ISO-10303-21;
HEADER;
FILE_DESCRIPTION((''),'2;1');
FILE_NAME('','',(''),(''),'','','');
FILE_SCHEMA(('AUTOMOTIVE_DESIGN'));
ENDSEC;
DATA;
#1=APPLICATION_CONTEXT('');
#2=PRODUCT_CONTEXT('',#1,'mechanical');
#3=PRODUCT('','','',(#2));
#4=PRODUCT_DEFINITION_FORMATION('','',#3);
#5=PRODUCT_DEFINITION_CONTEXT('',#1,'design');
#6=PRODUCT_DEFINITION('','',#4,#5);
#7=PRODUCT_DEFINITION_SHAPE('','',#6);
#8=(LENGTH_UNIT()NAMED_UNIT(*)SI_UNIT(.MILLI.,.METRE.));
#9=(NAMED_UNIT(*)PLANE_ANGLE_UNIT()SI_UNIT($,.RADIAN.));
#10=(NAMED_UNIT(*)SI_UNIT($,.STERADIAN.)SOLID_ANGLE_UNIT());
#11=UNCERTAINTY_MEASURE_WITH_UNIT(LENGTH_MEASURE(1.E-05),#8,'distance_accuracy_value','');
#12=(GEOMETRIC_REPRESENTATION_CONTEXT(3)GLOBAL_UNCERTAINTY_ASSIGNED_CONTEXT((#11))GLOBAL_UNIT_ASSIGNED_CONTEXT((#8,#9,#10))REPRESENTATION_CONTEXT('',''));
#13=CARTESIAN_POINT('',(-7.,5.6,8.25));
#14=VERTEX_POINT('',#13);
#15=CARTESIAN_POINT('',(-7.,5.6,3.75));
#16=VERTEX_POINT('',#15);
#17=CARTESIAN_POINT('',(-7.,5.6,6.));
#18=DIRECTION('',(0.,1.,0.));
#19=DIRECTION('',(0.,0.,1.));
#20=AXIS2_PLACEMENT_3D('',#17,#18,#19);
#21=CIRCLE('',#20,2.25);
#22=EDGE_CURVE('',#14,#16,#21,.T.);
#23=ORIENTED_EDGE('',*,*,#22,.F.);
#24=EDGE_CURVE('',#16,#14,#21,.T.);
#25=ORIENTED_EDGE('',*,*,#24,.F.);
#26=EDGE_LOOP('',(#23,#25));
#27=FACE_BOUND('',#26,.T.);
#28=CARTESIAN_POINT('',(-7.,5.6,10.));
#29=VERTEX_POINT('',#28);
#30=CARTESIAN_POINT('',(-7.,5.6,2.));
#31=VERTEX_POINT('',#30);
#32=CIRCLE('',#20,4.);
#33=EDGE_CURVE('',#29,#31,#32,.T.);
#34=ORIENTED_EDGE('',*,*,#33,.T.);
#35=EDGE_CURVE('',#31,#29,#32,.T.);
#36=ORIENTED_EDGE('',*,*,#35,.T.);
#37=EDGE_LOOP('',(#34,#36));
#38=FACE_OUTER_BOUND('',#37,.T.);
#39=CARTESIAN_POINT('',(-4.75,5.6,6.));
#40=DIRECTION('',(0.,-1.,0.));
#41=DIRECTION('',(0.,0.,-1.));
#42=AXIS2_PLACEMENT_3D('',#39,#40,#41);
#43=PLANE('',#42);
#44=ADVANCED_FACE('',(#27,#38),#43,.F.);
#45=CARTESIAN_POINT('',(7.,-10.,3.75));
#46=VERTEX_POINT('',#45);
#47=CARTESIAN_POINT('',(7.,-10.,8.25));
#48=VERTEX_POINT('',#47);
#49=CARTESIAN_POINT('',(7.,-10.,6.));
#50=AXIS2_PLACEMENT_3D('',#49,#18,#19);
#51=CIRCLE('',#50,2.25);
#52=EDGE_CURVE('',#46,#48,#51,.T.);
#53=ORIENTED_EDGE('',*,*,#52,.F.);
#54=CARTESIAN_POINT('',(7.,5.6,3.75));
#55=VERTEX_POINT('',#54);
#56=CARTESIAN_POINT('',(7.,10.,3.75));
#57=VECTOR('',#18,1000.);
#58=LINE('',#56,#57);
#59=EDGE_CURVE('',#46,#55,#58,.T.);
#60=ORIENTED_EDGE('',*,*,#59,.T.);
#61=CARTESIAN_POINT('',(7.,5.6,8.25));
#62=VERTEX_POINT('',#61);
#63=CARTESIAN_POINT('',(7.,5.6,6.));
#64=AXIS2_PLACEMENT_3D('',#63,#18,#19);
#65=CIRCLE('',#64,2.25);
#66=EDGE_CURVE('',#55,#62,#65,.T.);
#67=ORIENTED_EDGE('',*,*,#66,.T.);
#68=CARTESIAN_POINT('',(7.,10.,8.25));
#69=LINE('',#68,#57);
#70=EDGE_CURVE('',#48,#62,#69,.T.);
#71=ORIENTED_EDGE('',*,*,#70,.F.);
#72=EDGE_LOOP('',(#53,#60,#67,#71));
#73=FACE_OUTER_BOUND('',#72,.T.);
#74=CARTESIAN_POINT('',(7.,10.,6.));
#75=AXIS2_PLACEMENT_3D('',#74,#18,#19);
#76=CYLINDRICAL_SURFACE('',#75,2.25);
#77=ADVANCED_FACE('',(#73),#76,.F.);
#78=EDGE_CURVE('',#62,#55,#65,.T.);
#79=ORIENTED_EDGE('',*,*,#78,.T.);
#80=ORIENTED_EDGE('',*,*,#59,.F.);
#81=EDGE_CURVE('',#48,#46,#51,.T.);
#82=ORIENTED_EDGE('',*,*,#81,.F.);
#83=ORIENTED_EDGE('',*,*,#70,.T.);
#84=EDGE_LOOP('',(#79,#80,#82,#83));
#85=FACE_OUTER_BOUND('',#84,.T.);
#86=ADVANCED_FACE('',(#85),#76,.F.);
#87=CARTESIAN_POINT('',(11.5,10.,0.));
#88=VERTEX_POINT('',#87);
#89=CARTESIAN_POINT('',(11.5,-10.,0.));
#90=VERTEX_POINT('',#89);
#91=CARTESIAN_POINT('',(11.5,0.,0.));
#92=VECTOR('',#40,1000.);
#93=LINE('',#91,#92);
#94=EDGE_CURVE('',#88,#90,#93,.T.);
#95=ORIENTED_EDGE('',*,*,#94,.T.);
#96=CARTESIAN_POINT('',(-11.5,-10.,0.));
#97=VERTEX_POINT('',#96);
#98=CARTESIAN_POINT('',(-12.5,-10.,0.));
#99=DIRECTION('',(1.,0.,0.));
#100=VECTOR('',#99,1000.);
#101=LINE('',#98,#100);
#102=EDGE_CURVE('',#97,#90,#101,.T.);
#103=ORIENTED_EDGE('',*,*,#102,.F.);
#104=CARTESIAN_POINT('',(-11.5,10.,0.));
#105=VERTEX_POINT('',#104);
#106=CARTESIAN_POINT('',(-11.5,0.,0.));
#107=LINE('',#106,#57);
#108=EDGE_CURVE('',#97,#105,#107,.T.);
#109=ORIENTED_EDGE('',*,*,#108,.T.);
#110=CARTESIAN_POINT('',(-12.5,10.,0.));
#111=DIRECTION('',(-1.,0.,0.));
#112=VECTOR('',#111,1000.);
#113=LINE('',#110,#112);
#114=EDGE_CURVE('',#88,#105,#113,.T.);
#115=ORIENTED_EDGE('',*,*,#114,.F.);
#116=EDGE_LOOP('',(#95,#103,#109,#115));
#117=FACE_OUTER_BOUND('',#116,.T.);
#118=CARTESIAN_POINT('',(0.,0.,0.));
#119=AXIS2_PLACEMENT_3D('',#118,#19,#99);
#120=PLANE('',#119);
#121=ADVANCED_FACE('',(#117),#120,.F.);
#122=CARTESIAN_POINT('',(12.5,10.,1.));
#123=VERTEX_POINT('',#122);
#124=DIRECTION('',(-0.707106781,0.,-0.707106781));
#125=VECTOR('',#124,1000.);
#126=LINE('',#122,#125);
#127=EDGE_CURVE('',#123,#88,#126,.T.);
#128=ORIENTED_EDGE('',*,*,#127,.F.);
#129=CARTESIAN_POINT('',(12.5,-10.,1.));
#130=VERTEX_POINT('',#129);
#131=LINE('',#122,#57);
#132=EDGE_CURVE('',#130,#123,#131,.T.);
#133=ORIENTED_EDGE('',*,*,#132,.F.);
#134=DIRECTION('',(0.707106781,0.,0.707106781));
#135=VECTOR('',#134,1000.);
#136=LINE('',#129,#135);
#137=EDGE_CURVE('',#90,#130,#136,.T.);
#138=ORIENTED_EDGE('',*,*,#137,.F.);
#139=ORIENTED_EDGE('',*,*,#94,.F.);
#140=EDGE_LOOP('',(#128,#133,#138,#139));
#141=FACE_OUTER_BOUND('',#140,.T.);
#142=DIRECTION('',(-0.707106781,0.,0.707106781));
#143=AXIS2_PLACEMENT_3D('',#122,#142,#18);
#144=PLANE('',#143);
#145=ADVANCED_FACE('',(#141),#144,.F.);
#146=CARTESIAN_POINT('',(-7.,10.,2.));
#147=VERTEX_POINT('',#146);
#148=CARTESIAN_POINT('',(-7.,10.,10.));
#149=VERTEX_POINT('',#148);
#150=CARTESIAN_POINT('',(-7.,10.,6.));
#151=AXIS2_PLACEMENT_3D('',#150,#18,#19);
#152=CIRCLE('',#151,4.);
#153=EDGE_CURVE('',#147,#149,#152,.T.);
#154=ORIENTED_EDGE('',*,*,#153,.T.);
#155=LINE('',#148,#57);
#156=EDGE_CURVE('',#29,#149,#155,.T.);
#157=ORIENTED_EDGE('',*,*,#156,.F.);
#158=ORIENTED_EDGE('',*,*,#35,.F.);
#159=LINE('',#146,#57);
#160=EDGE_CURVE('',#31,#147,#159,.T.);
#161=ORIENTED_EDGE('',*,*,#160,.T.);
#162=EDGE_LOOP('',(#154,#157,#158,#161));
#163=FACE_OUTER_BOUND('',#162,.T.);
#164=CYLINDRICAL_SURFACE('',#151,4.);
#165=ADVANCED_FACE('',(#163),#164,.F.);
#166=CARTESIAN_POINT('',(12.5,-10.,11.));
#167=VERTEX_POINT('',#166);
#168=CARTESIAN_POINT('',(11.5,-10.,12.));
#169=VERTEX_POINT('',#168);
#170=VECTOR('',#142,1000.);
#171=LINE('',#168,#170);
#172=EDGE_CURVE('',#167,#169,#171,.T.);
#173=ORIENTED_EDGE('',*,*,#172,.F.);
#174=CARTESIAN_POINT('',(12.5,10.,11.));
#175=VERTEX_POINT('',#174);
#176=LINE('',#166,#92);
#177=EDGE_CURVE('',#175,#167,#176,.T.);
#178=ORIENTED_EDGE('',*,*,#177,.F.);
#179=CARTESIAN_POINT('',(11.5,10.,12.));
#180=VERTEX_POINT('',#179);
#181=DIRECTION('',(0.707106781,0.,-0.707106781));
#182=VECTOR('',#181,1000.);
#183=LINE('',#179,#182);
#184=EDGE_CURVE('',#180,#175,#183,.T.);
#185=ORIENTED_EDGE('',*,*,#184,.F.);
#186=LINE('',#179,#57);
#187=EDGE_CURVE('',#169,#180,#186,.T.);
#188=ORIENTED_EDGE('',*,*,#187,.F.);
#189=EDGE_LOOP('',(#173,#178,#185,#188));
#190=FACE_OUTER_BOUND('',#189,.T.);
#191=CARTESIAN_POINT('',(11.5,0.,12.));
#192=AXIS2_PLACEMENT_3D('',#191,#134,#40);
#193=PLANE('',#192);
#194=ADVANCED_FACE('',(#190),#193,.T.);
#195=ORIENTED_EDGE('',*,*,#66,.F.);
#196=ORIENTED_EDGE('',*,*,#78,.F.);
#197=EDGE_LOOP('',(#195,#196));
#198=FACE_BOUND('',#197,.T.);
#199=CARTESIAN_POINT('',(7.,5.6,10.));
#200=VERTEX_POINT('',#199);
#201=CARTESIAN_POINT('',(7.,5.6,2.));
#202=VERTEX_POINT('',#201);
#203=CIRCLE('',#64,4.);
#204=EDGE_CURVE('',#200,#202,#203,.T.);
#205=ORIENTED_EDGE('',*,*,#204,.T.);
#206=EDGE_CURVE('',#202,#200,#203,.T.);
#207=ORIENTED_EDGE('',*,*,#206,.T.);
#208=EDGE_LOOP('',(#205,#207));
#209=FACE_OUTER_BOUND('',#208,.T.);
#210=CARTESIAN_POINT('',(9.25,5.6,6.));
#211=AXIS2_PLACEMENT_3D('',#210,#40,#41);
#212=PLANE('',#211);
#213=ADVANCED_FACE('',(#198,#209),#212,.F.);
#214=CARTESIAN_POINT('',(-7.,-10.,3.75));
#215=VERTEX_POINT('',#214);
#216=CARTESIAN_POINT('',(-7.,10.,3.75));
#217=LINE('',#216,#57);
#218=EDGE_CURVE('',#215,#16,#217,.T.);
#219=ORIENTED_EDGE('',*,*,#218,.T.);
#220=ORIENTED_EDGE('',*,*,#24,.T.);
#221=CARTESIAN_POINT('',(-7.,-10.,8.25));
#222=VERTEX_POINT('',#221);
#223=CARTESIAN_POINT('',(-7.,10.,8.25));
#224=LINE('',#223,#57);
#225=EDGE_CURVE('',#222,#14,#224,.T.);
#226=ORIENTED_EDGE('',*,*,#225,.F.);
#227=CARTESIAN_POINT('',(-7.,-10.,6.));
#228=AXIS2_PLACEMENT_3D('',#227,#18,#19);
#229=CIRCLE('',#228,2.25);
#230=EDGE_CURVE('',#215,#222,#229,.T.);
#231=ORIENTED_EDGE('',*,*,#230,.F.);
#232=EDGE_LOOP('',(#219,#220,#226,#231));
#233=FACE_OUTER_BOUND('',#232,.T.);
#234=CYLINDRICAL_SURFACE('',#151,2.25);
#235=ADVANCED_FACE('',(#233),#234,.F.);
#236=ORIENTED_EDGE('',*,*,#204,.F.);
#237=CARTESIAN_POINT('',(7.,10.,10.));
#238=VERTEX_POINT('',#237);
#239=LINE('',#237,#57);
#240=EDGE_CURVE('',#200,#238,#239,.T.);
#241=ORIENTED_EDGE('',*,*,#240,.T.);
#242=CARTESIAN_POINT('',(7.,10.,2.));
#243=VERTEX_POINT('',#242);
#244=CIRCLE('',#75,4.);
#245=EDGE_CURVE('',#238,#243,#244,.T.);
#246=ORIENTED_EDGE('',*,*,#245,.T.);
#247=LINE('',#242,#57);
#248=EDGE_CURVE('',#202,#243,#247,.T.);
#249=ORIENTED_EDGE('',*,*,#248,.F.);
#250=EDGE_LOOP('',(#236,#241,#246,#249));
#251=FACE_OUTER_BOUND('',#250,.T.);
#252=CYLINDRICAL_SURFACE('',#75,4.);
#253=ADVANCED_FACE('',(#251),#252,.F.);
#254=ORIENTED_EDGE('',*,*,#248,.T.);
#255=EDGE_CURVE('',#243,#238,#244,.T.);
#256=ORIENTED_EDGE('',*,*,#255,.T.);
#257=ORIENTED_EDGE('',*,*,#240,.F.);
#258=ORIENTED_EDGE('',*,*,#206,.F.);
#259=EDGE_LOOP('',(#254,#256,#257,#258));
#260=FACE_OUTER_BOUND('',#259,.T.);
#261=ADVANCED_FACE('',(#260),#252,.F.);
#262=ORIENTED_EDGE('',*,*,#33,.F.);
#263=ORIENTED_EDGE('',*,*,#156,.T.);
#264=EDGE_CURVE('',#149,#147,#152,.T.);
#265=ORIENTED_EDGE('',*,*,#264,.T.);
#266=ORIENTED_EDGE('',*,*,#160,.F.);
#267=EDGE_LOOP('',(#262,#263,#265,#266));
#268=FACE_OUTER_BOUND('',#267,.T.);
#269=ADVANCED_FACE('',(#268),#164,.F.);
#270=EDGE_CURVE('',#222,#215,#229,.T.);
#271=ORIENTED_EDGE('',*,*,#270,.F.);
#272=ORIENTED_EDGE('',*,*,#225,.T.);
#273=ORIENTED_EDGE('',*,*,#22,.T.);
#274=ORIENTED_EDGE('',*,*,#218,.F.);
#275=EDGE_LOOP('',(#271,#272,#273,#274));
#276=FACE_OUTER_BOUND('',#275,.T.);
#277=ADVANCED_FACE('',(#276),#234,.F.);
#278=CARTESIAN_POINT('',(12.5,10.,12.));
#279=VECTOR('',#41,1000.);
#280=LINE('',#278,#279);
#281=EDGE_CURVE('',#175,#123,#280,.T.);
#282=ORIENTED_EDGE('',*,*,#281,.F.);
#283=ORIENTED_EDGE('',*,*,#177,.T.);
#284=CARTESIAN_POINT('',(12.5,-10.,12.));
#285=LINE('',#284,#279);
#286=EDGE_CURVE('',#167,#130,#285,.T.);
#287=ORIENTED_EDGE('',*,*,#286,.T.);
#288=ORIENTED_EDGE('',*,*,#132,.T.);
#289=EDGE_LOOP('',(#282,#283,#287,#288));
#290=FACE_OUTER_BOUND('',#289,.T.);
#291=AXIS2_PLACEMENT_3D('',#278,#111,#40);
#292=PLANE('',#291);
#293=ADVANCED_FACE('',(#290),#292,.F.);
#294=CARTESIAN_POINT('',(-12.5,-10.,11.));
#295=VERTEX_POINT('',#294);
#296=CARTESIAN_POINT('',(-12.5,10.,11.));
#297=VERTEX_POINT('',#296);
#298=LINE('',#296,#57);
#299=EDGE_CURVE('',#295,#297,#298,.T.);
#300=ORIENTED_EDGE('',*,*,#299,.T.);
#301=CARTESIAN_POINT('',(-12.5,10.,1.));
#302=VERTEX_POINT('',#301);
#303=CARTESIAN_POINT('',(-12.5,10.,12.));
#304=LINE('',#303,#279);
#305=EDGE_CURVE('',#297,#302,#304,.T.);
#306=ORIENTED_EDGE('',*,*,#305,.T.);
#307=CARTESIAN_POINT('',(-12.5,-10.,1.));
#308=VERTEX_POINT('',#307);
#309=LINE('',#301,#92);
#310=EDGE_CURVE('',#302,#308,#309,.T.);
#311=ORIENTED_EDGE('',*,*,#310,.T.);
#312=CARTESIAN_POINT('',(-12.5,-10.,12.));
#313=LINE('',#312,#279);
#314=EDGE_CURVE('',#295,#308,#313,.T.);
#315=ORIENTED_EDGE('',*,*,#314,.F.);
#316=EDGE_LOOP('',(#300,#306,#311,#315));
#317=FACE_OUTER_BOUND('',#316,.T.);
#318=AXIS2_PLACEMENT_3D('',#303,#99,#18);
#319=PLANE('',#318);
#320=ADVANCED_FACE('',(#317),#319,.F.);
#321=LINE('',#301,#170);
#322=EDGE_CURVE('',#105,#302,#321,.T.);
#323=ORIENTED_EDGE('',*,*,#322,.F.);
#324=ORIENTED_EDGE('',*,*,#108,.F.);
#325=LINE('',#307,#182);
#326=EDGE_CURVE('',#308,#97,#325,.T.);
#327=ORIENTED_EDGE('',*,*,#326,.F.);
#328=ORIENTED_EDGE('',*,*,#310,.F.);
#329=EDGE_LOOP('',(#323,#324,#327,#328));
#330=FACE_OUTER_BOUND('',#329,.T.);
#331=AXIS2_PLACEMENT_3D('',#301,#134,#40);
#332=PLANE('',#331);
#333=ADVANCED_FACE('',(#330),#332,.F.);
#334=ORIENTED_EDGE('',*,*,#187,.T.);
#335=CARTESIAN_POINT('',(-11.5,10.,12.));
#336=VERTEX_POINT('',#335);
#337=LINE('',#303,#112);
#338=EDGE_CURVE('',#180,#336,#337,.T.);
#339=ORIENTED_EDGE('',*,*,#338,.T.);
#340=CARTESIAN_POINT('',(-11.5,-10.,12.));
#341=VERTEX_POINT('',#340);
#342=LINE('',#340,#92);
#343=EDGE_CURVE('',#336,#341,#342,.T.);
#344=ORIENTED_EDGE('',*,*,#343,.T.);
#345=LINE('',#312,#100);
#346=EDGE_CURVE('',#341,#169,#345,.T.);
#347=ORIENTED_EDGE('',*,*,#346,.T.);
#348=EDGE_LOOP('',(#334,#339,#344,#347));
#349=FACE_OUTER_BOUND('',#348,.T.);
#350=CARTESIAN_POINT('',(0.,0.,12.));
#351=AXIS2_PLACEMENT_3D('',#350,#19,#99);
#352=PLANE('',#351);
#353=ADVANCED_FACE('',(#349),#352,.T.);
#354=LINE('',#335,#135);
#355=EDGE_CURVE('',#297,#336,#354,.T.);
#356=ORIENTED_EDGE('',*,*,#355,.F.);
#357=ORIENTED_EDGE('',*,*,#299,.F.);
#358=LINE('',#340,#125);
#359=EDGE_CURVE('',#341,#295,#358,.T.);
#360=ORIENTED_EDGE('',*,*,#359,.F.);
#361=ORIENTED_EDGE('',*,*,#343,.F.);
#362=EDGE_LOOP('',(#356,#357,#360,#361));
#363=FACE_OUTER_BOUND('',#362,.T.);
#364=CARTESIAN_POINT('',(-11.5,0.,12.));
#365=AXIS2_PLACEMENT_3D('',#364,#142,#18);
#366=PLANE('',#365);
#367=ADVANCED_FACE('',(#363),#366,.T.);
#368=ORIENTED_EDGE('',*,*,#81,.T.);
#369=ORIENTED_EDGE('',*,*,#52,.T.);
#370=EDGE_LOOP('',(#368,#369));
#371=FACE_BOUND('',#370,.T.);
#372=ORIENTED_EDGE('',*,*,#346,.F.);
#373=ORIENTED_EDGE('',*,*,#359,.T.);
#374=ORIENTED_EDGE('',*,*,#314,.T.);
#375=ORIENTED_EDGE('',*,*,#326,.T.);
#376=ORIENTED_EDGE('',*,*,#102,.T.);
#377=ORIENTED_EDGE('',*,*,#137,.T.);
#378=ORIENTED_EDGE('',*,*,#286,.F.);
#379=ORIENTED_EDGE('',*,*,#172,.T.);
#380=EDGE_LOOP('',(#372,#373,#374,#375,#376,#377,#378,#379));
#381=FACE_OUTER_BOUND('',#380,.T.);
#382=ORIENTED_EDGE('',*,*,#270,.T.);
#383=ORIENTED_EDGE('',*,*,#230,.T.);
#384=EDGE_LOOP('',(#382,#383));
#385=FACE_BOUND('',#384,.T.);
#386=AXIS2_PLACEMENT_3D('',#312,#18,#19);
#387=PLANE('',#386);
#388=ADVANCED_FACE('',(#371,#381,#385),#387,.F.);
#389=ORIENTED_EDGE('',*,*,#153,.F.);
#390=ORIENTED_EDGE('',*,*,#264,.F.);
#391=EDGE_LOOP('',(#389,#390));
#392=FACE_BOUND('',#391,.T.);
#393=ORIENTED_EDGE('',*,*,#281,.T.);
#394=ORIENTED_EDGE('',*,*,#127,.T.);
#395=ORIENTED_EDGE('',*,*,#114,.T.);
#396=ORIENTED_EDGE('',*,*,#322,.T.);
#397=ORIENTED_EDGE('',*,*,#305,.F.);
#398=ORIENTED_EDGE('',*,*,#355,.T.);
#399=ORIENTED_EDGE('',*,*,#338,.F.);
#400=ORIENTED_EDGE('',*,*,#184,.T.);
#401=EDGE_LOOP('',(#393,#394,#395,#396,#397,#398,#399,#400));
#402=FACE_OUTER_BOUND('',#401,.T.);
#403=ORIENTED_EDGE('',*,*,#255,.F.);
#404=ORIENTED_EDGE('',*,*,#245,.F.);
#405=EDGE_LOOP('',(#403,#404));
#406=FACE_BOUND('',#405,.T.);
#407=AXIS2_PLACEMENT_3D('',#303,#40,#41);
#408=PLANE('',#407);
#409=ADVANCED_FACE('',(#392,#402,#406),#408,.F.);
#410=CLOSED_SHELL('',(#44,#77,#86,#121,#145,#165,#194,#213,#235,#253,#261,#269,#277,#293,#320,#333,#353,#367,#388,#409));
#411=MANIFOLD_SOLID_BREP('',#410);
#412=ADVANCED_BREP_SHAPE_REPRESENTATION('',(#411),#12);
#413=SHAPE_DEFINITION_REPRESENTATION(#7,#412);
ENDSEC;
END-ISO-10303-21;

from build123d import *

# Parameters (mm, degrees)
SKETCH1_W                                           = 25
SKETCH1_H                                           = 20
BOSS_EXTRUDE1_DEPTH                                 = 12
CBORE_FOR_M4_HEX_SOCKET_HEAD_CAP_SCREW1_D           = 4.5
CBORE_FOR_M4_HEX_SOCKET_HEAD_CAP_SCREW1_CBORE_D     = 8
CBORE_FOR_M4_HEX_SOCKET_HEAD_CAP_SCREW1_CBORE_DEPTH = 4.4
CHAMFER1_SIZE                                       = 1


with BuildPart() as part:
    # Sketch1 → Boss-Extrude1 (new body)
    with BuildSketch(Plane.XY):
        Rectangle(SKETCH1_W, SKETCH1_H)
    extrude(amount=BOSS_EXTRUDE1_DEPTH)

    # CBORE for M4 Hex Socket Head Cap Screw1 (through all)
    with Locations(Plane(origin=(0, 10, 0), x_dir=(1, 0, 0), z_dir=(0, 1, 0))):
        with Locations((-7, -6), (7, -6)):
            CounterBoreHole(CBORE_FOR_M4_HEX_SOCKET_HEAD_CAP_SCREW1_D / 2, CBORE_FOR_M4_HEX_SOCKET_HEAD_CAP_SCREW1_CBORE_D / 2, CBORE_FOR_M4_HEX_SOCKET_HEAD_CAP_SCREW1_CBORE_DEPTH)

    # Chamfer1
    chamfer1_edges = [part.edges().sort_by_distance(p)[0] for p in [
        (-12.5, 0, 12),
        (12.5, 0, 12),
        (-12.5, 0, 0),
        (12.5, 0, 0),
    ]]
    chamfer(chamfer1_edges, length=CHAMFER1_SIZE)


solid = part.part
